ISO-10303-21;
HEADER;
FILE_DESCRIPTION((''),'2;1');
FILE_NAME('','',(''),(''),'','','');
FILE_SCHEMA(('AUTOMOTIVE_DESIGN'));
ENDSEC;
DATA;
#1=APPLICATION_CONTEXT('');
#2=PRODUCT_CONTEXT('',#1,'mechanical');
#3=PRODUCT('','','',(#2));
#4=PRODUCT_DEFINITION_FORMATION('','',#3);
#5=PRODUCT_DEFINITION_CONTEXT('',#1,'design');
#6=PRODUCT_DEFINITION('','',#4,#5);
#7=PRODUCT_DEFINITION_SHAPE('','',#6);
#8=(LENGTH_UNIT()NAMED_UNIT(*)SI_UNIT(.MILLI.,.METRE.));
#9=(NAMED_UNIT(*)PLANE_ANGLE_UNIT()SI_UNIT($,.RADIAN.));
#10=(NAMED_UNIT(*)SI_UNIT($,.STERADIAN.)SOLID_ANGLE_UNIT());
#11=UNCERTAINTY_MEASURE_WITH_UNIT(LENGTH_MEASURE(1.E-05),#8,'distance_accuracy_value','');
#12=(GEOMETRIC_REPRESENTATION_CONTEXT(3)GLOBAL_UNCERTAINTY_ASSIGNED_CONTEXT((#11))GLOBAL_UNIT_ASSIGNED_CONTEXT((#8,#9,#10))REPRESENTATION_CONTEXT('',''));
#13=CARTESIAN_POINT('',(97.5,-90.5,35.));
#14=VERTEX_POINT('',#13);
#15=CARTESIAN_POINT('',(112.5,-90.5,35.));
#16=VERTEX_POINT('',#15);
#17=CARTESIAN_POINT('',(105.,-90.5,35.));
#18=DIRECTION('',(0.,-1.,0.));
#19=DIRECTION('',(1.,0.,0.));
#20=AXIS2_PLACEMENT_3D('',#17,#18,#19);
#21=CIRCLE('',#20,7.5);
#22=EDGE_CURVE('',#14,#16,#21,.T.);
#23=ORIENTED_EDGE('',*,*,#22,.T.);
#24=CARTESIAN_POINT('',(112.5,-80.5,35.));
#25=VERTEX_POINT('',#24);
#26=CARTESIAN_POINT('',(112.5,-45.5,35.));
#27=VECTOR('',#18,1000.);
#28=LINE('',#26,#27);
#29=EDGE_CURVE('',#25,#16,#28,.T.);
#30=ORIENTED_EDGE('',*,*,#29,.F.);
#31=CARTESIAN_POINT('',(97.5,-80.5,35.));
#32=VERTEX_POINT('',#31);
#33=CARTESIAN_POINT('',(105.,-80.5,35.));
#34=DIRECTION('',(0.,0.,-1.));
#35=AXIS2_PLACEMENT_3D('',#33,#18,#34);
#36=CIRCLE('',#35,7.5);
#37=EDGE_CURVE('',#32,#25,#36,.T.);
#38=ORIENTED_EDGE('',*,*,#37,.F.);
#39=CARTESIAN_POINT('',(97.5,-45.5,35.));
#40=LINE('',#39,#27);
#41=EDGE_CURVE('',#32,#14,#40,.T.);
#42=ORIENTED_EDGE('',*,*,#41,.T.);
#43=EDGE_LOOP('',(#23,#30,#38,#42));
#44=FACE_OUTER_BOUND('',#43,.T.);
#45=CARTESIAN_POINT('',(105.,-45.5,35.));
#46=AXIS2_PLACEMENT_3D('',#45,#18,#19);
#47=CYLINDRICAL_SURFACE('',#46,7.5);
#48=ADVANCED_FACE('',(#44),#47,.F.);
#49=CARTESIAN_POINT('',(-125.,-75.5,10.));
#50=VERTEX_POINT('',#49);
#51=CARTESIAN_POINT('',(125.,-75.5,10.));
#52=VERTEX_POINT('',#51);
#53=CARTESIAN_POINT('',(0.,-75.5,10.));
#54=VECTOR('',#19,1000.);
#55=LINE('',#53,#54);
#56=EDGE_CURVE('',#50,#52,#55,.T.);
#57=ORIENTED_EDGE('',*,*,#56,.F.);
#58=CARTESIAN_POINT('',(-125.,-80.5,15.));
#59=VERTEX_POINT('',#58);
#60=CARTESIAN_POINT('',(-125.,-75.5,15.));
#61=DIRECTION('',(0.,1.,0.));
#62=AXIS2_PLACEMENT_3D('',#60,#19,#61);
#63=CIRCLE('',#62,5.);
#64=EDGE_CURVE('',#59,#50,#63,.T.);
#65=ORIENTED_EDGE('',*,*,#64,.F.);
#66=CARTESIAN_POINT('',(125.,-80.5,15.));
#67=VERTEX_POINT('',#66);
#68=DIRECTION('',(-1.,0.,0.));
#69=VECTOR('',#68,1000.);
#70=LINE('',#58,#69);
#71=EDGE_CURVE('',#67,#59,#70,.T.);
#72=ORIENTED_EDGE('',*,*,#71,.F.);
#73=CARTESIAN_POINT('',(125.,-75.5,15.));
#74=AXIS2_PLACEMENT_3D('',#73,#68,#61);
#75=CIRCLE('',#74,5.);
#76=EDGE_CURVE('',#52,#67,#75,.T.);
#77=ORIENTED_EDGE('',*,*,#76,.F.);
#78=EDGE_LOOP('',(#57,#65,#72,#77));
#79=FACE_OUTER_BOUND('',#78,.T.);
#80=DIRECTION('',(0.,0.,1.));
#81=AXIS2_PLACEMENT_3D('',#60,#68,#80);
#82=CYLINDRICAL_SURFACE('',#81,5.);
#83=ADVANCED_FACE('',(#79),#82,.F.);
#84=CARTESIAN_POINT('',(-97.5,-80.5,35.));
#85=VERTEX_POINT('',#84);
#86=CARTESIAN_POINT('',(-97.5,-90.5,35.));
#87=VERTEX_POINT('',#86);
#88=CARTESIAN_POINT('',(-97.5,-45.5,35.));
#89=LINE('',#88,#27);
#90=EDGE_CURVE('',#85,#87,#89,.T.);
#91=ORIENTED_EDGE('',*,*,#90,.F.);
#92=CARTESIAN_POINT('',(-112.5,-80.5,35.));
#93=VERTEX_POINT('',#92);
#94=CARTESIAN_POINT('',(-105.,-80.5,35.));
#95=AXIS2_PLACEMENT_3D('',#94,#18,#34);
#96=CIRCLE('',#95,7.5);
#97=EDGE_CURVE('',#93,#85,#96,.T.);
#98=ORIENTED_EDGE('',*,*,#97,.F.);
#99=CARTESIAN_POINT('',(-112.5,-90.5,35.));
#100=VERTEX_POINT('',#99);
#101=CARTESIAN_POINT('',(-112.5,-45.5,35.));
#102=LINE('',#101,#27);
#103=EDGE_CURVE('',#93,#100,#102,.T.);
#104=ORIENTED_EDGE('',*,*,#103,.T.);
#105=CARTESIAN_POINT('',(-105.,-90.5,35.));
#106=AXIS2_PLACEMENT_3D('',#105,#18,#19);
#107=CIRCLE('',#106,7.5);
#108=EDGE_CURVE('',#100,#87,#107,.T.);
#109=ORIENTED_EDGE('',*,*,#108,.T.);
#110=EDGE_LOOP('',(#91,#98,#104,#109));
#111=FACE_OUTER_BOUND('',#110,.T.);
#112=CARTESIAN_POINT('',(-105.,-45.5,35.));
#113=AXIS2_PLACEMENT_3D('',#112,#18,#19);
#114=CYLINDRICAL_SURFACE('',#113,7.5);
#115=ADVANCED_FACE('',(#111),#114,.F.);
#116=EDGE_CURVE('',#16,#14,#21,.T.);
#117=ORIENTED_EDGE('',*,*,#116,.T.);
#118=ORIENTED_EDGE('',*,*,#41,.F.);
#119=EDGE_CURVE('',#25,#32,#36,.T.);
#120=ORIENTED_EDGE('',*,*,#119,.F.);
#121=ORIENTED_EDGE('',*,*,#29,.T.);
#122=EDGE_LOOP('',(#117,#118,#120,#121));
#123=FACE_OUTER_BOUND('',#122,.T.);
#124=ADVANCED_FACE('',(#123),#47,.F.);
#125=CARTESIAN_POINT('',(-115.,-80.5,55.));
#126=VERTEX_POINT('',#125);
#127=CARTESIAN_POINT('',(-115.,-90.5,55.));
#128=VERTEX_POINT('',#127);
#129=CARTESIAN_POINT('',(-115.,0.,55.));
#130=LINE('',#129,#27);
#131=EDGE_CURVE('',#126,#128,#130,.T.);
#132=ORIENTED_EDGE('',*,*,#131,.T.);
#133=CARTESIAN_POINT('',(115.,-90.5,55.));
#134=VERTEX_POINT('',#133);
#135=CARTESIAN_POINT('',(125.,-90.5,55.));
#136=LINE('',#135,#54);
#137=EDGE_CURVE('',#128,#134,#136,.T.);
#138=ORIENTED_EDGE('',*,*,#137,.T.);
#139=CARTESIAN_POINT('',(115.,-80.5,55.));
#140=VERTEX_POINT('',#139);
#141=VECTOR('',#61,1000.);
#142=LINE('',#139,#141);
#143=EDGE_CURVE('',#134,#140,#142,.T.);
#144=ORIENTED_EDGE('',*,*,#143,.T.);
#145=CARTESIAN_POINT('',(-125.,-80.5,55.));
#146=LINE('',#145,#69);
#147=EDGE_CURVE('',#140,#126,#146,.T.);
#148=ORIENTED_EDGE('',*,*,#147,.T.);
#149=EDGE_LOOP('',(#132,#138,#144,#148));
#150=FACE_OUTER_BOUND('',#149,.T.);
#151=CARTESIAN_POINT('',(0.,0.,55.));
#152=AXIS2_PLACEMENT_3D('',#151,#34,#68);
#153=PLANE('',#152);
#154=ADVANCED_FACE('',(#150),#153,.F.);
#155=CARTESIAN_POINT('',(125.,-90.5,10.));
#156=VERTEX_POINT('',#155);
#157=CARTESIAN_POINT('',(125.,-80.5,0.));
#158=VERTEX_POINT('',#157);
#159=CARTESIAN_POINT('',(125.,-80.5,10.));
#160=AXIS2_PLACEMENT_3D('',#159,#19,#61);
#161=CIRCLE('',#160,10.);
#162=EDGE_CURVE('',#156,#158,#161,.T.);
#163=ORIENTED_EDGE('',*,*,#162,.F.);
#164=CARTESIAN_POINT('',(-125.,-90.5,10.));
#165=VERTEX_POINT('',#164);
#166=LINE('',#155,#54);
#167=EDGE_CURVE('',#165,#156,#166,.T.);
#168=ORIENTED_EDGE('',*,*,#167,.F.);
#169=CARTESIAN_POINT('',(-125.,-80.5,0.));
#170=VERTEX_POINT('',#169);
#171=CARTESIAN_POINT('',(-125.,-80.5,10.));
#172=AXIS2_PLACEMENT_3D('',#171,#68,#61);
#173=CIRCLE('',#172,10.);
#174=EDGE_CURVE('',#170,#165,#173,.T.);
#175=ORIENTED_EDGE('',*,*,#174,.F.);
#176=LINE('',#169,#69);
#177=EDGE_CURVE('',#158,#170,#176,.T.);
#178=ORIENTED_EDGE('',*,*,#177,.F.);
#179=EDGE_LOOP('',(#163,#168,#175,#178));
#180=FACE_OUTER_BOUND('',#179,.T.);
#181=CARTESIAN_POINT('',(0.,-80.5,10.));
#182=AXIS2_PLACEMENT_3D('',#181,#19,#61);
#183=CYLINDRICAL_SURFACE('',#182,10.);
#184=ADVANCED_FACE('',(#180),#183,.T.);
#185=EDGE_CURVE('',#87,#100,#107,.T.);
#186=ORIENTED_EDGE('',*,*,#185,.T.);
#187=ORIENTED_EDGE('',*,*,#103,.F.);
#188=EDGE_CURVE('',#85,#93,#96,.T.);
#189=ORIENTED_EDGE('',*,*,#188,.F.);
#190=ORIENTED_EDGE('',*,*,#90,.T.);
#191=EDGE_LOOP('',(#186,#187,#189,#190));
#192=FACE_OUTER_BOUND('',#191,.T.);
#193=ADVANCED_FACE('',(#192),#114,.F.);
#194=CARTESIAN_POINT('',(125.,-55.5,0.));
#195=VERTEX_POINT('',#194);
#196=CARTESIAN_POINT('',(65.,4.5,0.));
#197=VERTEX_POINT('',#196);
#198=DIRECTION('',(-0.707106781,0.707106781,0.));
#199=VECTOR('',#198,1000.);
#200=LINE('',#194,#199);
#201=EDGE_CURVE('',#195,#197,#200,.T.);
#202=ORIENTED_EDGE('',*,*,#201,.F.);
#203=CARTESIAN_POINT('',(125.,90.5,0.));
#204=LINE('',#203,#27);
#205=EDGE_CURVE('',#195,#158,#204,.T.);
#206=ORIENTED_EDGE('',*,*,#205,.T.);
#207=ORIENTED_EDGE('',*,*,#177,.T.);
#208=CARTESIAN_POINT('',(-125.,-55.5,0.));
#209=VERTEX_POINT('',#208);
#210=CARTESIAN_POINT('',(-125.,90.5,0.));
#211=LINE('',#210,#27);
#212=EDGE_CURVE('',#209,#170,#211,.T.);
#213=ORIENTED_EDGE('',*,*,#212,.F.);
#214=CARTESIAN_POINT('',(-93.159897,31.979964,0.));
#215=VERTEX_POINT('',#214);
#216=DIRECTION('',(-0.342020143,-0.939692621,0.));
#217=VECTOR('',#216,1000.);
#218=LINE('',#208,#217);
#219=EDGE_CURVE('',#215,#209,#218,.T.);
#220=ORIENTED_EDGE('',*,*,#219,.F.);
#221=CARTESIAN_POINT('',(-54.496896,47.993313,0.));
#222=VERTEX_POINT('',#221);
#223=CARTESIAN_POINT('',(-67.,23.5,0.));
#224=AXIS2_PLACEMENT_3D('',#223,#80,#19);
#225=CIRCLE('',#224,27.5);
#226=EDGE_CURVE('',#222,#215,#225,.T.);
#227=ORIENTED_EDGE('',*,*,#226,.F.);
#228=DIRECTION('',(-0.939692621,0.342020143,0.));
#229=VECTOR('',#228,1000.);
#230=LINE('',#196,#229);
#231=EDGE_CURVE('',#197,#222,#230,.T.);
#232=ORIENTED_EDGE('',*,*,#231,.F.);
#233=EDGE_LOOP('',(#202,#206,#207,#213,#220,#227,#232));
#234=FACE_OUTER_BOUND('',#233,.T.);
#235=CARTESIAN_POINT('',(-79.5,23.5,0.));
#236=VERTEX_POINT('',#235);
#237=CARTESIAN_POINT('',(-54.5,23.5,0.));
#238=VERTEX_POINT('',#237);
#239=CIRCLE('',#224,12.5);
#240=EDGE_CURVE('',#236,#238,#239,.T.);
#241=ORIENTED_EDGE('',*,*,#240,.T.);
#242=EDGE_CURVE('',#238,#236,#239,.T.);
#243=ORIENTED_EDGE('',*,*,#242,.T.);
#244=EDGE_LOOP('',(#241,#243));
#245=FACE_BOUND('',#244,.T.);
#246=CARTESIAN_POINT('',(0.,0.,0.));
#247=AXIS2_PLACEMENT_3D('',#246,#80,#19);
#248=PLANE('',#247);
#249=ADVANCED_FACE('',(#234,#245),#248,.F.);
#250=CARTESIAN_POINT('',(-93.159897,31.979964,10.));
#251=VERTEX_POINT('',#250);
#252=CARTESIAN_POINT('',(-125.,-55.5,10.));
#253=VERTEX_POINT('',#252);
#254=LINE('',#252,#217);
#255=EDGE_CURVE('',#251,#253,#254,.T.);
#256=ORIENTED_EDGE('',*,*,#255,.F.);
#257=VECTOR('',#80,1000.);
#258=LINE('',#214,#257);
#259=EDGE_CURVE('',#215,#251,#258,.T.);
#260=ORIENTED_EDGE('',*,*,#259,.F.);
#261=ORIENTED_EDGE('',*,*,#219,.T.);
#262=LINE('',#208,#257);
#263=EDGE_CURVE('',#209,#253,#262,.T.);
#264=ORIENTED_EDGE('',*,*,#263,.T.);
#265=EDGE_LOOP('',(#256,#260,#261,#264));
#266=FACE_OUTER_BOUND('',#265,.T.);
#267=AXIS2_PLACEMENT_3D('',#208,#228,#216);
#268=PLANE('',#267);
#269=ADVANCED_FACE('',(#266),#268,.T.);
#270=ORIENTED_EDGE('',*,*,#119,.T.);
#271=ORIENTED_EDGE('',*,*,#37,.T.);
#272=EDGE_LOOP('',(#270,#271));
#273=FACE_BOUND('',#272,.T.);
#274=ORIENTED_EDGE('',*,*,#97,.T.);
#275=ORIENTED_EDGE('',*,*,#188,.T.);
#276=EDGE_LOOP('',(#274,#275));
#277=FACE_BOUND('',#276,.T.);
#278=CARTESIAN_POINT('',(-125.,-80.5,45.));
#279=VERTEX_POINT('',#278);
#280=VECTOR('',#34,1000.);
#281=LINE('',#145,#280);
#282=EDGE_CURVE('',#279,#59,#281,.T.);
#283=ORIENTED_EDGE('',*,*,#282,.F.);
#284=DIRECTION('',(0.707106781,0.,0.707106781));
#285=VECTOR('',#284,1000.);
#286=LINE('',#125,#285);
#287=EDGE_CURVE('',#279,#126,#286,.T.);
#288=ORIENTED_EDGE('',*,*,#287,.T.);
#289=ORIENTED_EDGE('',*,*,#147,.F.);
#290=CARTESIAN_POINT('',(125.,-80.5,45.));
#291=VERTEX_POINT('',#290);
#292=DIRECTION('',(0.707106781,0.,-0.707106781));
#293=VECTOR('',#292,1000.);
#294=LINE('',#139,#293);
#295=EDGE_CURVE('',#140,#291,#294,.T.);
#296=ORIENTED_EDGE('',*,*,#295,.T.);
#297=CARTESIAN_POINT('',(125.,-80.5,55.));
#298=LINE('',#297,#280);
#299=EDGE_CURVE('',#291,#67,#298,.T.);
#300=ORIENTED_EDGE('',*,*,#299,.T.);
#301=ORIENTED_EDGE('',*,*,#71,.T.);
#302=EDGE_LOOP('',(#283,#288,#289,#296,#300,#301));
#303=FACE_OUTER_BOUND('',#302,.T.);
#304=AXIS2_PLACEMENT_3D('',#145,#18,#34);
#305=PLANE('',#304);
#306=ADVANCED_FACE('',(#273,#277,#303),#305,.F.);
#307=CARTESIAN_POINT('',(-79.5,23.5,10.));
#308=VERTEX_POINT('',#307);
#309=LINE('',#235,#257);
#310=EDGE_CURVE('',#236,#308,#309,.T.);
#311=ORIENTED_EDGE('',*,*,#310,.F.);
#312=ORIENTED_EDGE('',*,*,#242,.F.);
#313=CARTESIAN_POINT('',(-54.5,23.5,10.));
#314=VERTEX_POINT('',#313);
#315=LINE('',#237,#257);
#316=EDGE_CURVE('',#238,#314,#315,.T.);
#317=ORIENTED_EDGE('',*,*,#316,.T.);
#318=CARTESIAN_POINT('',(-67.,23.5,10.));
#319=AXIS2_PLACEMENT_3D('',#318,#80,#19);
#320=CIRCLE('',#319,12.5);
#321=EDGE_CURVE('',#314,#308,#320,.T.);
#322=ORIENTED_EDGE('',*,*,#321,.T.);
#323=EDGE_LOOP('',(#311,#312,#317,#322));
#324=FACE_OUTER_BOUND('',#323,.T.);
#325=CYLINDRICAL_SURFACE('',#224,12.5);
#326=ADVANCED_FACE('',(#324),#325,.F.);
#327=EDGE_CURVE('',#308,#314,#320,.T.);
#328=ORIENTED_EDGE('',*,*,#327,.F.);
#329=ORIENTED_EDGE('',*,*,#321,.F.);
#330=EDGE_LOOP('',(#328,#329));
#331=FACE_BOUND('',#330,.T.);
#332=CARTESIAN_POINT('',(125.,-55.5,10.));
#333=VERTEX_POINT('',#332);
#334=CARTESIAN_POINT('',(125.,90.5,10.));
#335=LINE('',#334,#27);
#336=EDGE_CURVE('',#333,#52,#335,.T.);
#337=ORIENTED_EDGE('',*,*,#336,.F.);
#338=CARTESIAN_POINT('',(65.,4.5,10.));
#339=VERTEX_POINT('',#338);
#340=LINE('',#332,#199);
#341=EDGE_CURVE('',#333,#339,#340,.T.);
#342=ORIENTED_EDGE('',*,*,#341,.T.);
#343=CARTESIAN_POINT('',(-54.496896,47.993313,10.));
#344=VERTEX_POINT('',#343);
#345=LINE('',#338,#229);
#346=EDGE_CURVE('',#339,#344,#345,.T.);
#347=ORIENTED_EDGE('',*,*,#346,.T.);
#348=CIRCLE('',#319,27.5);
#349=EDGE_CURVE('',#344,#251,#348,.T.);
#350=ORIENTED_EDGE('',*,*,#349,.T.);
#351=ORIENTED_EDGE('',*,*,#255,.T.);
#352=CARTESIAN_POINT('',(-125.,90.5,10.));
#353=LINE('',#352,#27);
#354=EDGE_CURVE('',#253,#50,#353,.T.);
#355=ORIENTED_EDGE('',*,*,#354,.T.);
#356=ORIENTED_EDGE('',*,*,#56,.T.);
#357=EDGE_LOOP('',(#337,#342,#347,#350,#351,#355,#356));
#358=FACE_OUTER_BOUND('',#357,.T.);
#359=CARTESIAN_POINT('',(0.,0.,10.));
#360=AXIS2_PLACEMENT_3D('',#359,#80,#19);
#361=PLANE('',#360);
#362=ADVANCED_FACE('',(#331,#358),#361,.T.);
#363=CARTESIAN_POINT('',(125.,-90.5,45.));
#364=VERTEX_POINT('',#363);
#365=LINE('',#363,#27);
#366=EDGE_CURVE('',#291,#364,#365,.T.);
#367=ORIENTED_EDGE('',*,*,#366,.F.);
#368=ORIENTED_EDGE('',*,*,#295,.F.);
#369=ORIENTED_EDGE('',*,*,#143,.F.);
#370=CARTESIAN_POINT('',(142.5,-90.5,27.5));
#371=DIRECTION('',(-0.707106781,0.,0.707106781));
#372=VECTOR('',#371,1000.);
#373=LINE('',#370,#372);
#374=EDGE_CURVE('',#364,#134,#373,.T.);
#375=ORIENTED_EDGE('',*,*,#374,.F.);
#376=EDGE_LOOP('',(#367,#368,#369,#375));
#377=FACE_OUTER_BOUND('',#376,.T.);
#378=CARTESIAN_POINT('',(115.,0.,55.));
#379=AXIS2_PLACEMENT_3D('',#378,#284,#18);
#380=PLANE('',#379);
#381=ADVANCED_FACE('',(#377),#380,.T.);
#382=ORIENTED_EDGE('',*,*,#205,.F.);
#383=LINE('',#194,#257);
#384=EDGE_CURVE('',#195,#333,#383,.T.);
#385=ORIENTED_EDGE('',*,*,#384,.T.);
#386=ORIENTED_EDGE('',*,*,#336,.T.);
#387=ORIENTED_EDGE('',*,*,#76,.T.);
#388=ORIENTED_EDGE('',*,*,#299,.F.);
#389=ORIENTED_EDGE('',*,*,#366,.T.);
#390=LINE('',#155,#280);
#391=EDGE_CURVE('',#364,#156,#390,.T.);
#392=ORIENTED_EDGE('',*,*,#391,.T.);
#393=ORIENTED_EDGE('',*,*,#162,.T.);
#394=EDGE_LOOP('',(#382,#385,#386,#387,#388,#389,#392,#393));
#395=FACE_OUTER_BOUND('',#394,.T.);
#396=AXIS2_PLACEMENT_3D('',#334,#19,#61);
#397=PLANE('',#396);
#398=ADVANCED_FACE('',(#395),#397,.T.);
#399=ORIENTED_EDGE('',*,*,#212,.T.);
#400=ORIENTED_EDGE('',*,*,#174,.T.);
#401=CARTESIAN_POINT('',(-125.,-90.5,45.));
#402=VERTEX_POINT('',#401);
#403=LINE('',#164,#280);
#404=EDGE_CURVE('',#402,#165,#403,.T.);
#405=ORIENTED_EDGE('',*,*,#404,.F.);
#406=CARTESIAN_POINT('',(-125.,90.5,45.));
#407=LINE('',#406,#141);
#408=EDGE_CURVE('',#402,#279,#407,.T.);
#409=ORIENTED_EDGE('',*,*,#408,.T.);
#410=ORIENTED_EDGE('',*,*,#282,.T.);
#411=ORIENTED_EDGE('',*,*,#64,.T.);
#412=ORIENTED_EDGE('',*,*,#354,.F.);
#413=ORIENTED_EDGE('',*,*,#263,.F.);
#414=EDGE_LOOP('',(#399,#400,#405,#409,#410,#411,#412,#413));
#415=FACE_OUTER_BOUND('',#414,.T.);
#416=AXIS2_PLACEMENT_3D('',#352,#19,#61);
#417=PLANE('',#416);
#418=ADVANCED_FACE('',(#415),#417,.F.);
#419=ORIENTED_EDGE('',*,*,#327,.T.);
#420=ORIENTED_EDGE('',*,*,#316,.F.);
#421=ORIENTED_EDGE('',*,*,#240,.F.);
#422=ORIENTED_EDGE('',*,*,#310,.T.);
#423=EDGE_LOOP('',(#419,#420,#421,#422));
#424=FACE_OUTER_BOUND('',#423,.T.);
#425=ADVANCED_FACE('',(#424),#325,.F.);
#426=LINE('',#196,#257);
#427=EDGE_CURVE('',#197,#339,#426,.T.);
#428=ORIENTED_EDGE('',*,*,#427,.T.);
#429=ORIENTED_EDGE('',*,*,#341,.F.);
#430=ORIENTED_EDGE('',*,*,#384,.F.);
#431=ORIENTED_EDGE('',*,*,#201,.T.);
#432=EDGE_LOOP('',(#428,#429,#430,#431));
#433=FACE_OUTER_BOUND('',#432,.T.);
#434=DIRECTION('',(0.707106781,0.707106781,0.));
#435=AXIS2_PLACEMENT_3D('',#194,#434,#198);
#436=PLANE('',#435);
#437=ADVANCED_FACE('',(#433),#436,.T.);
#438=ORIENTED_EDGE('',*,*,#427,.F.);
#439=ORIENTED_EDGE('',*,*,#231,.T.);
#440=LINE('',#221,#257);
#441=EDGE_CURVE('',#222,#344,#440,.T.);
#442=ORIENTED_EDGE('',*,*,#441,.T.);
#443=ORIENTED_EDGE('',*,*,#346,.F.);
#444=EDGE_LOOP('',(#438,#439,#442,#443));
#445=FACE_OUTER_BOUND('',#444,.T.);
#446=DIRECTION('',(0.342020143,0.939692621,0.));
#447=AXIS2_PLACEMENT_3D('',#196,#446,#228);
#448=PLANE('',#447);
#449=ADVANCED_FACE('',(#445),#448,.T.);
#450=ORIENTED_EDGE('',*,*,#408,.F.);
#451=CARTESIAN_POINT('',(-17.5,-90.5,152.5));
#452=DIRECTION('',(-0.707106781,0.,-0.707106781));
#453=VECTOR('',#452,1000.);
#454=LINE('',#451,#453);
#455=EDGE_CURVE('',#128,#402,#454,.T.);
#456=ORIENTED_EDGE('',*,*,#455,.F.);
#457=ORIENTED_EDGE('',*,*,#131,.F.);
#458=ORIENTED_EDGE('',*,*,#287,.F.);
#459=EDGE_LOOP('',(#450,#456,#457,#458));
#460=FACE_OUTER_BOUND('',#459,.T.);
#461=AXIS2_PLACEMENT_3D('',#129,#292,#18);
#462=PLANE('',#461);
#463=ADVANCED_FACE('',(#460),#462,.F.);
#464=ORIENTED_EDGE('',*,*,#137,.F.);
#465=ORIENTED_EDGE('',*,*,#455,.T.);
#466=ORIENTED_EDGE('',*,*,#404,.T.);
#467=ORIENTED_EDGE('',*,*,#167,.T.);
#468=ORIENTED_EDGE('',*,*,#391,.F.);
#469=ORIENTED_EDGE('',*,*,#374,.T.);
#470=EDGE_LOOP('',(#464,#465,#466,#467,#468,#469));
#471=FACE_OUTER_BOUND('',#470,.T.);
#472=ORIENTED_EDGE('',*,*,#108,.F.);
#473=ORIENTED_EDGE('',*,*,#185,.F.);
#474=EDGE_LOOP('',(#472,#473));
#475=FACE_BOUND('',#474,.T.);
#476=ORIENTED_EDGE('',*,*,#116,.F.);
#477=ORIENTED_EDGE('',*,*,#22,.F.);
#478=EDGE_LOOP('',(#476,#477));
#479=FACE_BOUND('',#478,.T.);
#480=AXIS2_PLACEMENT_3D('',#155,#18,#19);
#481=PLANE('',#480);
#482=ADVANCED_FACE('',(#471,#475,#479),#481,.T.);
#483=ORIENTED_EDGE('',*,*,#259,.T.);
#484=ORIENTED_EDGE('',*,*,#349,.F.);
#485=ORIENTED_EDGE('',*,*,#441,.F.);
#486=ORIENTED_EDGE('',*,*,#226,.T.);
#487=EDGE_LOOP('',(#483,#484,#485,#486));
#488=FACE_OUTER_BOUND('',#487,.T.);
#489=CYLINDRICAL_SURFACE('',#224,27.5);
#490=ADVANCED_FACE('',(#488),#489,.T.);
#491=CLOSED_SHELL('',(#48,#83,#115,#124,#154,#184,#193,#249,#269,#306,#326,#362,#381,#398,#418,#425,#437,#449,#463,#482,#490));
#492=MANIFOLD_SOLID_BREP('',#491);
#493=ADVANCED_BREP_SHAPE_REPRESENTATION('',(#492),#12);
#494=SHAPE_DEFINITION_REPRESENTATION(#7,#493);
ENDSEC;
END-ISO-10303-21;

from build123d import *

# Parameters (mm, degrees)
SKETCH1_W           = 250
SKETCH1_H           = 181
BOSS_EXTRUDE1_DEPTH = 10
SKETCH2_OUTSIDE_W   = 313.762
SKETCH2_OUTSIDE_H   = 244.762
CUT_EXTRUDE1_DEPTH  = 10
SKETCH3_R           = 12.5
CUT_EXTRUDE2_DEPTH  = 10
SKETCH6_W           = 250
SKETCH6_H           = 10
BOSS_EXTRUDE3_DEPTH = 45
FILLET3_R           = 5
FILLET4_R           = 10
SKETCH7_R           = 7.5
CUT_EXTRUDE4_DEPTH  = 45
CHAMFER2_SIZE       = 10


with BuildPart() as part:
    # Sketch1 → Boss-Extrude1 (new body)
    with BuildSketch(Plane.XY):
        Rectangle(SKETCH1_W, SKETCH1_H)
    extrude(amount=BOSS_EXTRUDE1_DEPTH)

    # Sketch2 outside → Cut-Extrude1 (cut)
    with BuildSketch(Plane.XY.offset(10)):
        Rectangle(SKETCH2_OUTSIDE_W, SKETCH2_OUTSIDE_H)
        with BuildLine():
            Line((-125, -55.5), (-93.159896838, 31.97996447))
            ThreePointArc((-93.159896838, 31.97996447), (-77.523014584, 48.907010136), (-54.496896373, 47.993313367))
            Line((-54.496896373, 47.993313367), (65, 4.5))
            Line((65, 4.5), (125, -55.5))
            Line((125, -55.5), (125, -90.5))
            Line((125, -90.5), (-125, -90.5))
            Line((-125, -90.5), (-125, -55.5))
        make_face(mode=Mode.SUBTRACT)
    extrude(amount=-CUT_EXTRUDE1_DEPTH, mode=Mode.SUBTRACT)

    # Sketch3 → Cut-Extrude2 (cut)
    with BuildSketch(Plane.XY.offset(10)):
        with Locations((-67, 23.5)):
            Circle(SKETCH3_R)
    extrude(amount=-CUT_EXTRUDE2_DEPTH, mode=Mode.SUBTRACT)

    # Sketch6 → Boss-Extrude3 (add)
    with BuildSketch(Plane.XY.offset(10)):
        with Locations((0, -85.5)):
            Rectangle(SKETCH6_W, SKETCH6_H)
    extrude(amount=BOSS_EXTRUDE3_DEPTH)

    # Fillet3
    fillet3_edges = [part.edges().sort_by_distance(p)[0] for p in [
        (0, -80.5, 10),
    ]]
    fillet(fillet3_edges, radius=FILLET3_R)

    # Fillet4
    fillet4_edges = [part.edges().sort_by_distance(p)[0] for p in [
        (0, -90.5, 0),
    ]]
    fillet(fillet4_edges, radius=FILLET4_R)

    # Sketch7 → Cut-Extrude4 (cut)
    with BuildSketch(Plane.XZ.offset(90.5)):
        with Locations((-105, 35)):
            Circle(SKETCH7_R)
        with Locations((105, 35)):
            Circle(SKETCH7_R)
    extrude(amount=-CUT_EXTRUDE4_DEPTH, mode=Mode.SUBTRACT)

    # Chamfer2
    chamfer2_edges = [part.edges().sort_by_distance(p)[0] for p in [
        (-125, -85.5, 55),
        (125, -85.5, 55),
    ]]
    chamfer(chamfer2_edges, length=CHAMFER2_SIZE)


solid = part.part
